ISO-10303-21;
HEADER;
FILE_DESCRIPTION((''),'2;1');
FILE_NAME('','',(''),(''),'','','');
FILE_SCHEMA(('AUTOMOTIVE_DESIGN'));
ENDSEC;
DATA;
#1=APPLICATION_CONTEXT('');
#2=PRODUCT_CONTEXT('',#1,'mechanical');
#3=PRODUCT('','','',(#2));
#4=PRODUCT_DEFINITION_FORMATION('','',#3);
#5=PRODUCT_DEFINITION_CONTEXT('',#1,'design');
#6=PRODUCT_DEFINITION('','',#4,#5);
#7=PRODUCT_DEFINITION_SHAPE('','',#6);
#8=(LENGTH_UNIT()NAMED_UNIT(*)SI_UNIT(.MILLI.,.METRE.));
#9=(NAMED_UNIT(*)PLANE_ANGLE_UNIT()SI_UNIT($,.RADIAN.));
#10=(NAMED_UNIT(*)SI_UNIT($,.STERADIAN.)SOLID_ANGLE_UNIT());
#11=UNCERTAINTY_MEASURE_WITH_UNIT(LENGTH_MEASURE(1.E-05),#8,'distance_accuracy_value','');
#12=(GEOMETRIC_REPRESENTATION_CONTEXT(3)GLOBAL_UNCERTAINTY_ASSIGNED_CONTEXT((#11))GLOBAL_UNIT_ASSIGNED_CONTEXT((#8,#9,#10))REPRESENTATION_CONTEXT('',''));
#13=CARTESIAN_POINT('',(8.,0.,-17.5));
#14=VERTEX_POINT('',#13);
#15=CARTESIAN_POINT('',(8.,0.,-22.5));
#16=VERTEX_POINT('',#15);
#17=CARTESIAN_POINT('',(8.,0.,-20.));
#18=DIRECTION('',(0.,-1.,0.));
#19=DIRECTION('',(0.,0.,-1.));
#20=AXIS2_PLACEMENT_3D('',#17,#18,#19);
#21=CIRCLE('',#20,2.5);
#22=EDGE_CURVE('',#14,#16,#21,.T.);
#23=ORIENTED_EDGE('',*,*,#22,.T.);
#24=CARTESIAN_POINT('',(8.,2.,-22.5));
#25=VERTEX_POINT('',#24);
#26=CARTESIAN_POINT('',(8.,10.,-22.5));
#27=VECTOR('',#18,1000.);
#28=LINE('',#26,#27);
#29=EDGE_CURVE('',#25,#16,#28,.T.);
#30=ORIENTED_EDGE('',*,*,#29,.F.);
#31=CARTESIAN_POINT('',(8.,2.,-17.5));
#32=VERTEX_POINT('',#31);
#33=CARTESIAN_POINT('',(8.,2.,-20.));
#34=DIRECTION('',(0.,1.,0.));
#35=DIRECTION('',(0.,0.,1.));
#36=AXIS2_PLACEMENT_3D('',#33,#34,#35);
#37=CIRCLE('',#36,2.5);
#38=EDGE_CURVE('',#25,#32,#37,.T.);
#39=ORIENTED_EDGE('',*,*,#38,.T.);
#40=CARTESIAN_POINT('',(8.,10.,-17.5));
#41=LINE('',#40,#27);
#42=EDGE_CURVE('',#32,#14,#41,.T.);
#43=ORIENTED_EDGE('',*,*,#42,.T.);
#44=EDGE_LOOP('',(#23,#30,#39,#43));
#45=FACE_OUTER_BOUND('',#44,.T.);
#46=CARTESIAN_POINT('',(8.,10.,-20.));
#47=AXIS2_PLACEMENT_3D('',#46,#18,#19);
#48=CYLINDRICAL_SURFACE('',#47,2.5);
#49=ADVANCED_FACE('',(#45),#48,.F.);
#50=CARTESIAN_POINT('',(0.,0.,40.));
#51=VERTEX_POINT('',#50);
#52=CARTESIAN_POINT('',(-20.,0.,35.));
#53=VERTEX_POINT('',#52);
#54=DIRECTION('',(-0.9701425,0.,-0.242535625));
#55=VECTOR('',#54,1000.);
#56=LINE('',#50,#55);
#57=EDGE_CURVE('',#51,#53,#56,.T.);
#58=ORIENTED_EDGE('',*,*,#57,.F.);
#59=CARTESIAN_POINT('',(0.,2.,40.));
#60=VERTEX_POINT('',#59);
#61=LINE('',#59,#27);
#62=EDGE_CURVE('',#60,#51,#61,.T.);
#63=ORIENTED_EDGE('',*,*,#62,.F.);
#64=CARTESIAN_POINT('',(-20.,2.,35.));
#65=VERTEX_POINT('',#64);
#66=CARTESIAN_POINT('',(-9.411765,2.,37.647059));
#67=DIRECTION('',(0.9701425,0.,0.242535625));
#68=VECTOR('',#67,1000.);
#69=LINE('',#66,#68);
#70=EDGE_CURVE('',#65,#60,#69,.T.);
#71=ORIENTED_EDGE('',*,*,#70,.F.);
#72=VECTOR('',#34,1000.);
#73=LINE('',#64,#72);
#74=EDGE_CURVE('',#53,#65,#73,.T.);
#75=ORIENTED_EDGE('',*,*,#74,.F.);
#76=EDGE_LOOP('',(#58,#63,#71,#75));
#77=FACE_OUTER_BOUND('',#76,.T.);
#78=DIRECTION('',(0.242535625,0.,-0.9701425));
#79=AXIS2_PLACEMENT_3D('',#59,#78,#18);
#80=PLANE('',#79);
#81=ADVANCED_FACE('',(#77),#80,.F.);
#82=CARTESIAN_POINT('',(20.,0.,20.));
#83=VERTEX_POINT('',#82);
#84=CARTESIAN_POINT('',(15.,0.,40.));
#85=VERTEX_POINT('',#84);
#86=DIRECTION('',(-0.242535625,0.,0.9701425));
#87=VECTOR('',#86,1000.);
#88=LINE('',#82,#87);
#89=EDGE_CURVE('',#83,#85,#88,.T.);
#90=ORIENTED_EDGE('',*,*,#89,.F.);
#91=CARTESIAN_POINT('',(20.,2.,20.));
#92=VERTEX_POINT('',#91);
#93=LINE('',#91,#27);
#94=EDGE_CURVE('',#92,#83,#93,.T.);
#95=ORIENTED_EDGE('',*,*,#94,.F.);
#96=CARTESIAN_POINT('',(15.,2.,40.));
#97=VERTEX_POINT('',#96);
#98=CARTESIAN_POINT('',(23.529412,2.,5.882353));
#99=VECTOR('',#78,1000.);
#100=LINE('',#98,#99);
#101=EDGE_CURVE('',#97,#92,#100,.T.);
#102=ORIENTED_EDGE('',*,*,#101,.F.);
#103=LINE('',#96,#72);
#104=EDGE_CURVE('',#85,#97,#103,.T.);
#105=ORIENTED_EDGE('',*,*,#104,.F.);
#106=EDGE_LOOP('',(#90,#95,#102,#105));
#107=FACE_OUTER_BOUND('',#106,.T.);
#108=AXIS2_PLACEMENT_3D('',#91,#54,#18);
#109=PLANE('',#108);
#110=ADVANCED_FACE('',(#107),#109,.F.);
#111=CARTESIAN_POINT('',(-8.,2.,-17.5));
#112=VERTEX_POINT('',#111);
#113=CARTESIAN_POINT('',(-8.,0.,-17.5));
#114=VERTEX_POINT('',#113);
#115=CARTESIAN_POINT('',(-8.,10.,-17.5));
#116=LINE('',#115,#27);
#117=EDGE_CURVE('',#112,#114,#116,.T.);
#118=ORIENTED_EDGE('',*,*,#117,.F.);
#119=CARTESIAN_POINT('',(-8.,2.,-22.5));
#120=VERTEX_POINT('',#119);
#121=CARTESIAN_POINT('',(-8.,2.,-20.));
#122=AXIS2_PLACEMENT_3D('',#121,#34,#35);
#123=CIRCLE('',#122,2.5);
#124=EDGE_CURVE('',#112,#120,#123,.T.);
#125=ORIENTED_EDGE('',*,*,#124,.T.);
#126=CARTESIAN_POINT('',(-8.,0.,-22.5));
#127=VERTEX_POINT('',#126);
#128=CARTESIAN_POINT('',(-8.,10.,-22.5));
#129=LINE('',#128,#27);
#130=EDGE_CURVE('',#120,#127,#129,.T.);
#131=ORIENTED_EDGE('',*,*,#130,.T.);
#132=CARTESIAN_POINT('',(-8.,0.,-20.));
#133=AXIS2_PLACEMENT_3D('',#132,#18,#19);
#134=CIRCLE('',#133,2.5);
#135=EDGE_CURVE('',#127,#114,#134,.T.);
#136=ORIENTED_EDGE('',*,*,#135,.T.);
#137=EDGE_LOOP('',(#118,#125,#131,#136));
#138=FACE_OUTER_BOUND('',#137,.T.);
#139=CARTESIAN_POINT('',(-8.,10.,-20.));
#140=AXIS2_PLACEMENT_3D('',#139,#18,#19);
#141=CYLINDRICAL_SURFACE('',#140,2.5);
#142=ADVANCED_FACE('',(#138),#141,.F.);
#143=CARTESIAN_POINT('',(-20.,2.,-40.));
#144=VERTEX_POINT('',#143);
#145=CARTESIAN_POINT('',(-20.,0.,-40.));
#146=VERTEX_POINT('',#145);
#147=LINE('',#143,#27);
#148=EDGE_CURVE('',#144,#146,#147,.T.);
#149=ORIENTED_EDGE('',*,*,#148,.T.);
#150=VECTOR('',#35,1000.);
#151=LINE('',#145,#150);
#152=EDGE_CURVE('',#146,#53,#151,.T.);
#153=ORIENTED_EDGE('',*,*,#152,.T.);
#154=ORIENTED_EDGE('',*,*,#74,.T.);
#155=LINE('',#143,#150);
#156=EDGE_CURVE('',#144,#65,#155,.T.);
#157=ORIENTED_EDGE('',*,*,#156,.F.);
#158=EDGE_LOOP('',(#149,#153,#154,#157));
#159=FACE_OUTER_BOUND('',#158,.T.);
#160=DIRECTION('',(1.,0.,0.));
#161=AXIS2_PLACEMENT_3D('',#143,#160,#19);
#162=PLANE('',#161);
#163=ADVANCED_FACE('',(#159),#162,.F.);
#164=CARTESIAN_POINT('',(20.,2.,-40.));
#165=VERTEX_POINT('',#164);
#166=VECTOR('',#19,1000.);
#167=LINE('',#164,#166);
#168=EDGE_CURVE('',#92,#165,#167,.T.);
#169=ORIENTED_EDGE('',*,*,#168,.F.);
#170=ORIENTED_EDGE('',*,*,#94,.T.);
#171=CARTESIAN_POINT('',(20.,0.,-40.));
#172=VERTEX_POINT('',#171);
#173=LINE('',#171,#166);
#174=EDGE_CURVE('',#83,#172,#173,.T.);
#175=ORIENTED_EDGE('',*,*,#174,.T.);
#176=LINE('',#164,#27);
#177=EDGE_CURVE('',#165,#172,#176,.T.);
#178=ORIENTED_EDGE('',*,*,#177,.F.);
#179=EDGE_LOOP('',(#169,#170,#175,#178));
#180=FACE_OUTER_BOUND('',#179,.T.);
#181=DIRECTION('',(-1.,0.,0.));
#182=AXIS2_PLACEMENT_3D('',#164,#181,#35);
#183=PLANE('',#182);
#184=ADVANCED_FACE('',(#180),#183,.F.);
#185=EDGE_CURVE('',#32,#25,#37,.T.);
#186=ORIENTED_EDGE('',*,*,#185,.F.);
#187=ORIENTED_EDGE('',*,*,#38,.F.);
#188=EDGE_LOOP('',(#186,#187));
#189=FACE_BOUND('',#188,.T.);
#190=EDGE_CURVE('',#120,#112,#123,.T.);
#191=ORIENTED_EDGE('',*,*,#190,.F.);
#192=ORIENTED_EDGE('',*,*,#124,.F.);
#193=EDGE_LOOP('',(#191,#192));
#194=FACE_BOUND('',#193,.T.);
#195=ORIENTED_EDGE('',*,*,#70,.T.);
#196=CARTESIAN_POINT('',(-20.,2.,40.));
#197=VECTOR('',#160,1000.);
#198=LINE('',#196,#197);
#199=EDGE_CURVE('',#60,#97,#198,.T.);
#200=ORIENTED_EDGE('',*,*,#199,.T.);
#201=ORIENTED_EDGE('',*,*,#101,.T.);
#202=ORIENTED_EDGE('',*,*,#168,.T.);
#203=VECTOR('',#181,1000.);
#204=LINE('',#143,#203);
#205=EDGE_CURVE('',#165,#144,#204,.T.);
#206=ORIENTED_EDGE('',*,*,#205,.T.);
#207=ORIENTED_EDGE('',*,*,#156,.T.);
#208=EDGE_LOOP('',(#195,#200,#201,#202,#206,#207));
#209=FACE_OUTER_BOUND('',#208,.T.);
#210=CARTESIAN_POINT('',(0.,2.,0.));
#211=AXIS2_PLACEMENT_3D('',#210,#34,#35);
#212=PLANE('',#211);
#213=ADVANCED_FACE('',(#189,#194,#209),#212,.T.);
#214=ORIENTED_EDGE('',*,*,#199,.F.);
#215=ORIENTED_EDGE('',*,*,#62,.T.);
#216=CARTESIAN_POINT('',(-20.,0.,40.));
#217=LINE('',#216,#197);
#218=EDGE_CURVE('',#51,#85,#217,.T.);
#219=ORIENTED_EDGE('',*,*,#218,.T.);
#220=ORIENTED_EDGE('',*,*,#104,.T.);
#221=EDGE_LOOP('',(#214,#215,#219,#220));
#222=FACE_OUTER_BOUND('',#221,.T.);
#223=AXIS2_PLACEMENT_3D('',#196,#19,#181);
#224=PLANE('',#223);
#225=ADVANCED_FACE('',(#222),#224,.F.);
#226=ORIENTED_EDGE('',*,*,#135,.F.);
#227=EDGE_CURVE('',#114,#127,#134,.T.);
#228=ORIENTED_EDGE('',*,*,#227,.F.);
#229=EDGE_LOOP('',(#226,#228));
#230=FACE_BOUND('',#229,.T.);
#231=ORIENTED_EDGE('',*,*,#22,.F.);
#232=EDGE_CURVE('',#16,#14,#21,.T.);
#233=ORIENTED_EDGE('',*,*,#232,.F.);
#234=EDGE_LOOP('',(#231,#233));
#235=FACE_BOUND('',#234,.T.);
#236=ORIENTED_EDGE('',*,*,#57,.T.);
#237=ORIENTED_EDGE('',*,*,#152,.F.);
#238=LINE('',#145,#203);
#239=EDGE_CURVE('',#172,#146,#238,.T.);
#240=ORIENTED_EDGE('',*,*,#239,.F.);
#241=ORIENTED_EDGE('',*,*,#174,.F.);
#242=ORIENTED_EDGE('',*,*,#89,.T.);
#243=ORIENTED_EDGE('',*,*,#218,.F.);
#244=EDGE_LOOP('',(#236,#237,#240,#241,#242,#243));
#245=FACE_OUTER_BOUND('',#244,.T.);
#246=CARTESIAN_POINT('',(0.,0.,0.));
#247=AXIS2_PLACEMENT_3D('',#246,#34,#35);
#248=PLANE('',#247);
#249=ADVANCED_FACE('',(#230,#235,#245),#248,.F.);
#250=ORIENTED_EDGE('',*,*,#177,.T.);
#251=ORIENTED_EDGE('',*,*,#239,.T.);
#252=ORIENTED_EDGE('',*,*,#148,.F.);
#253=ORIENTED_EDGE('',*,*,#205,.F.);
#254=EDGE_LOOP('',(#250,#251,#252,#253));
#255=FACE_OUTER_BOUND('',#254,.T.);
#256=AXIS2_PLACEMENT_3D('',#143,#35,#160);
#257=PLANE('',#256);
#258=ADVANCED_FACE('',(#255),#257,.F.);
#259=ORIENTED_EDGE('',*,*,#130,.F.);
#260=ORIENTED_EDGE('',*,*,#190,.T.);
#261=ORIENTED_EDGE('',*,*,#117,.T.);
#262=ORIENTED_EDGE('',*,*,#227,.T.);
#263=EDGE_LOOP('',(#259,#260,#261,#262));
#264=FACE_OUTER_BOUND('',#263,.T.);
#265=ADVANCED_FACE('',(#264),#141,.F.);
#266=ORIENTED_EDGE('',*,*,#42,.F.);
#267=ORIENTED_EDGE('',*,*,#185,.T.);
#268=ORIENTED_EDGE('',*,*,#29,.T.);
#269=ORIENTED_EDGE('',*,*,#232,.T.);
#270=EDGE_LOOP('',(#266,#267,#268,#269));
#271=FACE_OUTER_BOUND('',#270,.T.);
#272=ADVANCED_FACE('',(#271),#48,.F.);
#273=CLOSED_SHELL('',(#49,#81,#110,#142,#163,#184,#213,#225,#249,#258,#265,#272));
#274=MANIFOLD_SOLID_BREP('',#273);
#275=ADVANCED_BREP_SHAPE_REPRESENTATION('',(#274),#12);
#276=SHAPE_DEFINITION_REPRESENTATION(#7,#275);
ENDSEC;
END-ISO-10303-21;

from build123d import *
from OCP.BRepFilletAPI import BRepFilletAPI_MakeChamfer

# Parameters (mm, degrees)
SKETCH1_W           = 40
SKETCH1_H           = 80
BOSS_EXTRUDE1_DEPTH = 2
SKETCH2_R           = 2.5
CUT_EXTRUDE1_DEPTH  = 10
CHAMFER1_SIZE       = 5
CHAMFER1_SIZE2      = 20


with BuildPart() as part:
    # Sketch1 → Boss-Extrude1 (new body)
    with BuildSketch(Plane(origin=(0, 0, 0), x_dir=(1, 0, 0), z_dir=(0, 1, 0))):
        Rectangle(SKETCH1_W, SKETCH1_H)
    extrude(amount=BOSS_EXTRUDE1_DEPTH)

    # Sketch2 → Cut-Extrude1 (cut)
    with BuildSketch(Plane.XZ):
        with Locations(Location((8, -20, 0), (0, 0, 270))):
            Circle(SKETCH2_R)
        with Locations(Location((-8, -20, 0), (0, 0, 270))):
            Circle(SKETCH2_R)
    extrude(amount=-CUT_EXTRUDE1_DEPTH, mode=Mode.SUBTRACT)

    # Chamfer1: one chamfer whose edges measure the first distance from different faces: ONE call of the kernel's chamfer builder (chamfer() names one face for all edges)
    chamfer1_edges_1 = [part.edges().sort_by_distance(p)[0] for p in [
        (20, 1, 40),
    ]]
    chamfer1_side_1 = [part.faces().sort_by_distance(p)[0] for p in [
        (0, 1, 40),
    ]]
    chamfer1_edges_2 = [part.edges().sort_by_distance(p)[0] for p in [
        (-20, 1, 40),
    ]]
    chamfer1_side_2 = [part.faces().sort_by_distance(p)[0] for p in [
        (-20, 1, 0),
    ]]
    chamfer1 = BRepFilletAPI_MakeChamfer(part.part.solid().wrapped)
    for e in chamfer1_edges_1:
        chamfer1.Add(CHAMFER1_SIZE, CHAMFER1_SIZE2, e.wrapped, chamfer1_side_1[0].wrapped)  # the first distance lies on this face
    for e in chamfer1_edges_2:
        chamfer1.Add(CHAMFER1_SIZE, CHAMFER1_SIZE2, e.wrapped, chamfer1_side_2[0].wrapped)  # the first distance lies on this face
    add(Compound.cast(chamfer1.Shape()), mode=Mode.REPLACE)


solid = part.part
